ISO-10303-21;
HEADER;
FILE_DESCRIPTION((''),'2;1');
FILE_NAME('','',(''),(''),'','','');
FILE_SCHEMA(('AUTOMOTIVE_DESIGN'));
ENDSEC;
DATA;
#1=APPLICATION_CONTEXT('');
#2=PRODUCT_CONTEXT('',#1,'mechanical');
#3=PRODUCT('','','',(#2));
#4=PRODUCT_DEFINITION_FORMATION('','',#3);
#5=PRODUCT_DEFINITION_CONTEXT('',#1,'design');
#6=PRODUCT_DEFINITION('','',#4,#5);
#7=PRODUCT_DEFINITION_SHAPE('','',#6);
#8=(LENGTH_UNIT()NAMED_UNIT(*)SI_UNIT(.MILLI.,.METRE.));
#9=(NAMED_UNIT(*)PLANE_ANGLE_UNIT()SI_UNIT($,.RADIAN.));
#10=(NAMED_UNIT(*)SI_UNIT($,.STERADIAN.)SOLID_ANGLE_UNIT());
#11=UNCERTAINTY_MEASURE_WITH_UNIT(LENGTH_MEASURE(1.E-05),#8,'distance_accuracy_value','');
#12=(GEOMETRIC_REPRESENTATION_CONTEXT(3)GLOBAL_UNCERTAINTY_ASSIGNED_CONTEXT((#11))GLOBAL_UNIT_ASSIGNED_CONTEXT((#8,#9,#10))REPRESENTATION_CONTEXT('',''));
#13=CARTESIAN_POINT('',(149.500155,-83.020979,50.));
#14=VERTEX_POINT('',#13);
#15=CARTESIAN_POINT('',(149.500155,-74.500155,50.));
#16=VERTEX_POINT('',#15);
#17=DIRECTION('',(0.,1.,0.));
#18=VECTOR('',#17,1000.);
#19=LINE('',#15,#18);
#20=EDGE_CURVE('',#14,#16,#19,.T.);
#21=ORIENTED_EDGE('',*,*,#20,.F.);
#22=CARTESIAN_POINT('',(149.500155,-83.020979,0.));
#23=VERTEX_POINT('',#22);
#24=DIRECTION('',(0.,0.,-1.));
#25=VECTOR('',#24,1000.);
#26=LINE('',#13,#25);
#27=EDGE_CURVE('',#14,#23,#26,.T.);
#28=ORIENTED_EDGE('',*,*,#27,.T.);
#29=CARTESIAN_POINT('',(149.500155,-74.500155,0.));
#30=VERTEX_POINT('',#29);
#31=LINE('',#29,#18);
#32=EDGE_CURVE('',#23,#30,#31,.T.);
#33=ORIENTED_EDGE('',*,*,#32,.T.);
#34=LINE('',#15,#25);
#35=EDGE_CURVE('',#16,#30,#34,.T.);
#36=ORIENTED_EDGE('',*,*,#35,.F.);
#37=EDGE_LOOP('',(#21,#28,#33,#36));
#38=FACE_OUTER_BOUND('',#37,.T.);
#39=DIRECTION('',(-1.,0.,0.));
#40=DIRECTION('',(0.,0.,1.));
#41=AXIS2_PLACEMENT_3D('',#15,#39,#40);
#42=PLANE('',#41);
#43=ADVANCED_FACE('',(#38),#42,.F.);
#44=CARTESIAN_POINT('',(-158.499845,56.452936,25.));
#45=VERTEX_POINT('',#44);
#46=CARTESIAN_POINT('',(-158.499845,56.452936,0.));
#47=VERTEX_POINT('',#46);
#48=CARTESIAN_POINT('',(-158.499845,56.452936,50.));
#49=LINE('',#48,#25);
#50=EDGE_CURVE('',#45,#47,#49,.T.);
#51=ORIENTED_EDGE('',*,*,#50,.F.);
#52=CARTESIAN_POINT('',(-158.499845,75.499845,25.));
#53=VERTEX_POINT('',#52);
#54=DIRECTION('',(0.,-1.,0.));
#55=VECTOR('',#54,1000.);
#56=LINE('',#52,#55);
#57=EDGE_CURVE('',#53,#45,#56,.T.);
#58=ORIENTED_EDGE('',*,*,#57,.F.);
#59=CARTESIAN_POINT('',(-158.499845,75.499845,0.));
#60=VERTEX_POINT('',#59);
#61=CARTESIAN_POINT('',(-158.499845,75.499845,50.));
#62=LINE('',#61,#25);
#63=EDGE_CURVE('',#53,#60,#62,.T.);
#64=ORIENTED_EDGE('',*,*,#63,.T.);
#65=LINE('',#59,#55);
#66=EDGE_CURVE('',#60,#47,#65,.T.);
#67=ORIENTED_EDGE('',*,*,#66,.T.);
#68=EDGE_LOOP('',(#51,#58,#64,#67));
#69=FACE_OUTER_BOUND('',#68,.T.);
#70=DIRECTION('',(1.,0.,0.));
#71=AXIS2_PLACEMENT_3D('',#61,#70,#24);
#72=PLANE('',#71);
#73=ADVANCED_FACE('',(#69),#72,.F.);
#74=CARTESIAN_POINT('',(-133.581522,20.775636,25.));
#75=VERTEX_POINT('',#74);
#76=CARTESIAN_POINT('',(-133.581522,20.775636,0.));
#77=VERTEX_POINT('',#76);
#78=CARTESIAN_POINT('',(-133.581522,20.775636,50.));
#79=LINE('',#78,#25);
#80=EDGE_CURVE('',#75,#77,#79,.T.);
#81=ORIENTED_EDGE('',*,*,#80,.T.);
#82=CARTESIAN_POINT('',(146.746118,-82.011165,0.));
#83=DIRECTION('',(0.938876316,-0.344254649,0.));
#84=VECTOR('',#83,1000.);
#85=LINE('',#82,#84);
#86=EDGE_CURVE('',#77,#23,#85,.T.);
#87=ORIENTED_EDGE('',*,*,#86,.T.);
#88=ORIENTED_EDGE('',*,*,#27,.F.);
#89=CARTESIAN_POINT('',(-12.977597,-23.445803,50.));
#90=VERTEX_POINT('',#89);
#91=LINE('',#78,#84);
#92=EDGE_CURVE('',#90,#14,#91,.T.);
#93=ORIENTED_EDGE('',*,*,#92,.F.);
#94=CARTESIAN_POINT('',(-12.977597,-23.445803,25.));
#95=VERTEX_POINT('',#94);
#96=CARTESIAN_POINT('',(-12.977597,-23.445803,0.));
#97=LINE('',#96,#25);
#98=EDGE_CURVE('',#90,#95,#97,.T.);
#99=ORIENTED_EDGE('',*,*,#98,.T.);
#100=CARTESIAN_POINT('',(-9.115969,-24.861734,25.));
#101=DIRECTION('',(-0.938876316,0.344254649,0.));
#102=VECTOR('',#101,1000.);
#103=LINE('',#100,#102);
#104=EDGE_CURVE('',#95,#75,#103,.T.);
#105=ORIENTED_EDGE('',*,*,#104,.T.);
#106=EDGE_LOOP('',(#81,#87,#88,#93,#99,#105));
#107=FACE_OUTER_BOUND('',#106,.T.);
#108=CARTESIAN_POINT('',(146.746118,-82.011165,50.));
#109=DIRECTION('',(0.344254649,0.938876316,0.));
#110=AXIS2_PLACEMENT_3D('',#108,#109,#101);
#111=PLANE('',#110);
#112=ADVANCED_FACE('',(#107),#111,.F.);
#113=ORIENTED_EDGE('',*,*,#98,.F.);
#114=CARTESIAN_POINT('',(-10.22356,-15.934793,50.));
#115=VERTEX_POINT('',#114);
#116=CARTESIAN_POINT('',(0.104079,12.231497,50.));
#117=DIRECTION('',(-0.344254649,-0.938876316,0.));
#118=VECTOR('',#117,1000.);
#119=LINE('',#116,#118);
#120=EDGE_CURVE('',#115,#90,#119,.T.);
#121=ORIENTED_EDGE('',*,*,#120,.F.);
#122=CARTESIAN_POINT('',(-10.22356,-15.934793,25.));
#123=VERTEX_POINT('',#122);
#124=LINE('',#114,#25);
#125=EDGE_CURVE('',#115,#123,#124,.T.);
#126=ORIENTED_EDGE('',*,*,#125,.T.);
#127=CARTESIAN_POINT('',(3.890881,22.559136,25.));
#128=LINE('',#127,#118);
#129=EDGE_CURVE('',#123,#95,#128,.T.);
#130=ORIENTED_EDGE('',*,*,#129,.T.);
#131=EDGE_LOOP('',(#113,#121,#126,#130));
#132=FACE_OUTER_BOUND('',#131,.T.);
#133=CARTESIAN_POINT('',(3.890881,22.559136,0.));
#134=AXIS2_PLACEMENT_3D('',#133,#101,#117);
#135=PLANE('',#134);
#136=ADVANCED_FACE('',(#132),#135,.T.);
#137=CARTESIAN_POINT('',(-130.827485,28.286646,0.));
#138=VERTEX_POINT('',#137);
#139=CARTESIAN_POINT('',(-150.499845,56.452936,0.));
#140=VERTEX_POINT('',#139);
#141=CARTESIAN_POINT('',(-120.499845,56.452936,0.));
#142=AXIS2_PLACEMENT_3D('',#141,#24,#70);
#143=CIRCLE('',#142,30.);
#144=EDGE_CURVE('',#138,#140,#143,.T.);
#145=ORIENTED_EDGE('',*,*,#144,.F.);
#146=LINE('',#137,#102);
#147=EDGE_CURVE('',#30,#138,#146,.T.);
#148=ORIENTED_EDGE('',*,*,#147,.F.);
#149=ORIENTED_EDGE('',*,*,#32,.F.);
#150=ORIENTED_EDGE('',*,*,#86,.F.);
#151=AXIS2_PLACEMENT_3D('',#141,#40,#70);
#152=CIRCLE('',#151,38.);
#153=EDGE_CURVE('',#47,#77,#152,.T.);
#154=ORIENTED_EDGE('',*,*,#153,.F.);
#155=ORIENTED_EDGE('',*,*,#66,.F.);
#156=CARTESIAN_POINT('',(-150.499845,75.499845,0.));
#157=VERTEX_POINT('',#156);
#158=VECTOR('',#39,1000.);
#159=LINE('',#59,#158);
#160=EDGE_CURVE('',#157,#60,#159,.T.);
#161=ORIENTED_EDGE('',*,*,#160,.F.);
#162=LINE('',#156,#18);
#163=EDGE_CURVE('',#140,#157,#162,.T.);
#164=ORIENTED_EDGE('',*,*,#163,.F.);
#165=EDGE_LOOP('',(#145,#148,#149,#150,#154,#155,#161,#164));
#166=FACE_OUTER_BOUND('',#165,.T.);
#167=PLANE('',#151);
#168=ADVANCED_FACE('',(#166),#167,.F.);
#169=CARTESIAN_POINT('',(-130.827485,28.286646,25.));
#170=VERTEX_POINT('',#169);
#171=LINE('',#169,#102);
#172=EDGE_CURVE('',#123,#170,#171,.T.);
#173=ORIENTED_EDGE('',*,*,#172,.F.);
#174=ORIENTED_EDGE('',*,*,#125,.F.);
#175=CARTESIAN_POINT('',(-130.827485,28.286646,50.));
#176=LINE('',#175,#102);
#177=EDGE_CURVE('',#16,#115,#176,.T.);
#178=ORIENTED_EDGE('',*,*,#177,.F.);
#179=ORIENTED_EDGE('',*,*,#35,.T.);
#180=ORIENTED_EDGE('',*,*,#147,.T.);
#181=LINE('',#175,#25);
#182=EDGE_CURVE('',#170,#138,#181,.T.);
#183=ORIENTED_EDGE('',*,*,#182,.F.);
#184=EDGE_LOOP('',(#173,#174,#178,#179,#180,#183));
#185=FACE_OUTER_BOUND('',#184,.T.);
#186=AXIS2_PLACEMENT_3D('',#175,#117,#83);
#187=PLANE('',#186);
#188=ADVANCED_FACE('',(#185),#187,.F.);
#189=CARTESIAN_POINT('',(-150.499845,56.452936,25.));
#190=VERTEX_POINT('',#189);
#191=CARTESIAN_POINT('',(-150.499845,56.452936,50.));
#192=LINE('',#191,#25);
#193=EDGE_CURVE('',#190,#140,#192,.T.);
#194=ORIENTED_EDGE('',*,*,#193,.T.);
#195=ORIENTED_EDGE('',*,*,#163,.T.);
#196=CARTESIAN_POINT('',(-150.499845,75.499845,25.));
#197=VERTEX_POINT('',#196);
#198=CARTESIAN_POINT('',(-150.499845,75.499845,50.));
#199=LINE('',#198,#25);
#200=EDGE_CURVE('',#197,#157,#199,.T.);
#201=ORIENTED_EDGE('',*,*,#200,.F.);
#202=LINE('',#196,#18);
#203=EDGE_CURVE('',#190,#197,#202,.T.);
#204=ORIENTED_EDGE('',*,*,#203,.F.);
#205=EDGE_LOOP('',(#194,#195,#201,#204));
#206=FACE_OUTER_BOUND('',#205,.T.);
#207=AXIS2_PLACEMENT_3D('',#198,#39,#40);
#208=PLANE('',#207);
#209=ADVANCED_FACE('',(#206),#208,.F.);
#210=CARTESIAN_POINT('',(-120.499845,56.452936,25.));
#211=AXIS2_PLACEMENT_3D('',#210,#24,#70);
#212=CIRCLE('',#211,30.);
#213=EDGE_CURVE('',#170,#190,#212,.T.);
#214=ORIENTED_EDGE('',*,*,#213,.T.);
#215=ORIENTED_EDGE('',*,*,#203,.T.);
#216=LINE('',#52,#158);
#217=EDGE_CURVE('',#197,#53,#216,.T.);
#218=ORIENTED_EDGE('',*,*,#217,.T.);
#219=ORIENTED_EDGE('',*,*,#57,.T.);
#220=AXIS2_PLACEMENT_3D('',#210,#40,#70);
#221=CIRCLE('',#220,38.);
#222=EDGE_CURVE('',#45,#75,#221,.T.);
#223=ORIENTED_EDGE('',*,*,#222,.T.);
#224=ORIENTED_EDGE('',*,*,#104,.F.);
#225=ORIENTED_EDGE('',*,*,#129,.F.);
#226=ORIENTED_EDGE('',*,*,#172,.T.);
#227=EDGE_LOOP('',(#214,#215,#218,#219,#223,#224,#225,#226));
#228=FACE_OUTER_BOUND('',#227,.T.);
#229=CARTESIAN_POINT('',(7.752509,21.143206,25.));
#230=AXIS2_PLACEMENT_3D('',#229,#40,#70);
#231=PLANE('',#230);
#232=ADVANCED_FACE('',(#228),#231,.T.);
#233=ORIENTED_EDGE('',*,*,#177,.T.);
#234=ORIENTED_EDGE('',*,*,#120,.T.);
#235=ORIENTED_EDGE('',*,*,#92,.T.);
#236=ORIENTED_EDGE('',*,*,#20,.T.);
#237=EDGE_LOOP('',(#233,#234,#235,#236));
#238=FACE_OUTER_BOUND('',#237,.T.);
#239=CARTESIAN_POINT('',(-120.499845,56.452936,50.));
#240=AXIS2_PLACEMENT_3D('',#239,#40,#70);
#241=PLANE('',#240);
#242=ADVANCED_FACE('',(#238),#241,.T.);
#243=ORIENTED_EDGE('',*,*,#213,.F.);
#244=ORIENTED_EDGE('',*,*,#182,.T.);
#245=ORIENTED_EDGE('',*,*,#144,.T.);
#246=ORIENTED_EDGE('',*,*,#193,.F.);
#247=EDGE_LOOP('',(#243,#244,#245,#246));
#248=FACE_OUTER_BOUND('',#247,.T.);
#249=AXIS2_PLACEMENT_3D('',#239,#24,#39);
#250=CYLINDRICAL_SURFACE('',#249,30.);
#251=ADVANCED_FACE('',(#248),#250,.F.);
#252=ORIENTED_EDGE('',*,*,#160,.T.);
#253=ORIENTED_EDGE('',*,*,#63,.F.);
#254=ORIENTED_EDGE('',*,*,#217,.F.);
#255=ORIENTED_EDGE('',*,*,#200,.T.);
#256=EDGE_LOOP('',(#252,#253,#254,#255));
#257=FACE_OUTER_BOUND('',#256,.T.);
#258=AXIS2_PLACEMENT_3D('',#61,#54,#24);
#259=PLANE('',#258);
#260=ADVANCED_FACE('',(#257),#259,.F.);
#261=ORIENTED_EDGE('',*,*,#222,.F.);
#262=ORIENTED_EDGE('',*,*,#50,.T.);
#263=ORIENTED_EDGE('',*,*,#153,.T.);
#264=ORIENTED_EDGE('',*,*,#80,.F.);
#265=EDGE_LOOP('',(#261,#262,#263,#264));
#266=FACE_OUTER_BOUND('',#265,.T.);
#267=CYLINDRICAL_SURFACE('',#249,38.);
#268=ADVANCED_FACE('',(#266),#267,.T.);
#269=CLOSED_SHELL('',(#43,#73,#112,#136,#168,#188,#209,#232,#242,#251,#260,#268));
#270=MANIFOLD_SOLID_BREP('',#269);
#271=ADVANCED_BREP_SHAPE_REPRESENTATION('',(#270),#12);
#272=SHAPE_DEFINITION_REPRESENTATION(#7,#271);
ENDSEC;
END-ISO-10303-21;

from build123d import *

# Parameters (mm, degrees)
EXTRUDE_1_DEPTH     = 50
SKETCH_2_W          = 128.455604429
SKETCH_2_H          = 25
SKETCH_2_W_2        = 42.23428711
CUT_EXTRUDE_1_DEPTH = 49


with BuildPart() as part:
    # 草图1 → 凸台-拉伸1 (new body)
    with BuildSketch(Plane.XY):
        with BuildLine():
            Line((-158.499845276, 75.499845276), (-158.499845276, 56.452935893))
            ThreePointArc((-158.499845276, 56.452935893), (-151.653526546, 34.694072336), (-133.581521944, 20.77563589))
            Line((-133.581521944, 20.77563589), (146.746117531, -82.011165251))
            Line((146.746117531, -82.011165251), (149.500154724, -83.020978889))
            Line((149.500154724, -83.020978889), (149.500154724, -74.500154724))
            Line((149.500154724, -74.500154724), (-130.827484751, 28.286646417))
            ThreePointArc((-130.827484751, 28.286646417), (-145.094856805, 39.274885717), (-150.499845276, 56.452935893))
            Line((-150.499845276, 56.452935893), (-150.499845276, 75.499845276))
            Line((-150.499845276, 75.499845276), (-158.499845276, 75.499845276))
        make_face()
    extrude(amount=EXTRUDE_1_DEPTH)

    # 草图2 → 切除-拉伸1 (cut)
    with BuildSketch(Plane(origin=(-9.115968963, -24.861733537, 0), x_dir=(0.9388763158866098, -0.3442546491584201, 0), z_dir=(-0.3442546491584201, -0.9388763158866098, 0))):
        with Locations((-68.340834223, 37.5)):
            Rectangle(SKETCH_2_W, SKETCH_2_H)
        with Locations((-153.685779993, 37.5)):
            Rectangle(SKETCH_2_W_2, SKETCH_2_H)
    extrude(amount=-CUT_EXTRUDE_1_DEPTH, mode=Mode.SUBTRACT)


solid = part.part
